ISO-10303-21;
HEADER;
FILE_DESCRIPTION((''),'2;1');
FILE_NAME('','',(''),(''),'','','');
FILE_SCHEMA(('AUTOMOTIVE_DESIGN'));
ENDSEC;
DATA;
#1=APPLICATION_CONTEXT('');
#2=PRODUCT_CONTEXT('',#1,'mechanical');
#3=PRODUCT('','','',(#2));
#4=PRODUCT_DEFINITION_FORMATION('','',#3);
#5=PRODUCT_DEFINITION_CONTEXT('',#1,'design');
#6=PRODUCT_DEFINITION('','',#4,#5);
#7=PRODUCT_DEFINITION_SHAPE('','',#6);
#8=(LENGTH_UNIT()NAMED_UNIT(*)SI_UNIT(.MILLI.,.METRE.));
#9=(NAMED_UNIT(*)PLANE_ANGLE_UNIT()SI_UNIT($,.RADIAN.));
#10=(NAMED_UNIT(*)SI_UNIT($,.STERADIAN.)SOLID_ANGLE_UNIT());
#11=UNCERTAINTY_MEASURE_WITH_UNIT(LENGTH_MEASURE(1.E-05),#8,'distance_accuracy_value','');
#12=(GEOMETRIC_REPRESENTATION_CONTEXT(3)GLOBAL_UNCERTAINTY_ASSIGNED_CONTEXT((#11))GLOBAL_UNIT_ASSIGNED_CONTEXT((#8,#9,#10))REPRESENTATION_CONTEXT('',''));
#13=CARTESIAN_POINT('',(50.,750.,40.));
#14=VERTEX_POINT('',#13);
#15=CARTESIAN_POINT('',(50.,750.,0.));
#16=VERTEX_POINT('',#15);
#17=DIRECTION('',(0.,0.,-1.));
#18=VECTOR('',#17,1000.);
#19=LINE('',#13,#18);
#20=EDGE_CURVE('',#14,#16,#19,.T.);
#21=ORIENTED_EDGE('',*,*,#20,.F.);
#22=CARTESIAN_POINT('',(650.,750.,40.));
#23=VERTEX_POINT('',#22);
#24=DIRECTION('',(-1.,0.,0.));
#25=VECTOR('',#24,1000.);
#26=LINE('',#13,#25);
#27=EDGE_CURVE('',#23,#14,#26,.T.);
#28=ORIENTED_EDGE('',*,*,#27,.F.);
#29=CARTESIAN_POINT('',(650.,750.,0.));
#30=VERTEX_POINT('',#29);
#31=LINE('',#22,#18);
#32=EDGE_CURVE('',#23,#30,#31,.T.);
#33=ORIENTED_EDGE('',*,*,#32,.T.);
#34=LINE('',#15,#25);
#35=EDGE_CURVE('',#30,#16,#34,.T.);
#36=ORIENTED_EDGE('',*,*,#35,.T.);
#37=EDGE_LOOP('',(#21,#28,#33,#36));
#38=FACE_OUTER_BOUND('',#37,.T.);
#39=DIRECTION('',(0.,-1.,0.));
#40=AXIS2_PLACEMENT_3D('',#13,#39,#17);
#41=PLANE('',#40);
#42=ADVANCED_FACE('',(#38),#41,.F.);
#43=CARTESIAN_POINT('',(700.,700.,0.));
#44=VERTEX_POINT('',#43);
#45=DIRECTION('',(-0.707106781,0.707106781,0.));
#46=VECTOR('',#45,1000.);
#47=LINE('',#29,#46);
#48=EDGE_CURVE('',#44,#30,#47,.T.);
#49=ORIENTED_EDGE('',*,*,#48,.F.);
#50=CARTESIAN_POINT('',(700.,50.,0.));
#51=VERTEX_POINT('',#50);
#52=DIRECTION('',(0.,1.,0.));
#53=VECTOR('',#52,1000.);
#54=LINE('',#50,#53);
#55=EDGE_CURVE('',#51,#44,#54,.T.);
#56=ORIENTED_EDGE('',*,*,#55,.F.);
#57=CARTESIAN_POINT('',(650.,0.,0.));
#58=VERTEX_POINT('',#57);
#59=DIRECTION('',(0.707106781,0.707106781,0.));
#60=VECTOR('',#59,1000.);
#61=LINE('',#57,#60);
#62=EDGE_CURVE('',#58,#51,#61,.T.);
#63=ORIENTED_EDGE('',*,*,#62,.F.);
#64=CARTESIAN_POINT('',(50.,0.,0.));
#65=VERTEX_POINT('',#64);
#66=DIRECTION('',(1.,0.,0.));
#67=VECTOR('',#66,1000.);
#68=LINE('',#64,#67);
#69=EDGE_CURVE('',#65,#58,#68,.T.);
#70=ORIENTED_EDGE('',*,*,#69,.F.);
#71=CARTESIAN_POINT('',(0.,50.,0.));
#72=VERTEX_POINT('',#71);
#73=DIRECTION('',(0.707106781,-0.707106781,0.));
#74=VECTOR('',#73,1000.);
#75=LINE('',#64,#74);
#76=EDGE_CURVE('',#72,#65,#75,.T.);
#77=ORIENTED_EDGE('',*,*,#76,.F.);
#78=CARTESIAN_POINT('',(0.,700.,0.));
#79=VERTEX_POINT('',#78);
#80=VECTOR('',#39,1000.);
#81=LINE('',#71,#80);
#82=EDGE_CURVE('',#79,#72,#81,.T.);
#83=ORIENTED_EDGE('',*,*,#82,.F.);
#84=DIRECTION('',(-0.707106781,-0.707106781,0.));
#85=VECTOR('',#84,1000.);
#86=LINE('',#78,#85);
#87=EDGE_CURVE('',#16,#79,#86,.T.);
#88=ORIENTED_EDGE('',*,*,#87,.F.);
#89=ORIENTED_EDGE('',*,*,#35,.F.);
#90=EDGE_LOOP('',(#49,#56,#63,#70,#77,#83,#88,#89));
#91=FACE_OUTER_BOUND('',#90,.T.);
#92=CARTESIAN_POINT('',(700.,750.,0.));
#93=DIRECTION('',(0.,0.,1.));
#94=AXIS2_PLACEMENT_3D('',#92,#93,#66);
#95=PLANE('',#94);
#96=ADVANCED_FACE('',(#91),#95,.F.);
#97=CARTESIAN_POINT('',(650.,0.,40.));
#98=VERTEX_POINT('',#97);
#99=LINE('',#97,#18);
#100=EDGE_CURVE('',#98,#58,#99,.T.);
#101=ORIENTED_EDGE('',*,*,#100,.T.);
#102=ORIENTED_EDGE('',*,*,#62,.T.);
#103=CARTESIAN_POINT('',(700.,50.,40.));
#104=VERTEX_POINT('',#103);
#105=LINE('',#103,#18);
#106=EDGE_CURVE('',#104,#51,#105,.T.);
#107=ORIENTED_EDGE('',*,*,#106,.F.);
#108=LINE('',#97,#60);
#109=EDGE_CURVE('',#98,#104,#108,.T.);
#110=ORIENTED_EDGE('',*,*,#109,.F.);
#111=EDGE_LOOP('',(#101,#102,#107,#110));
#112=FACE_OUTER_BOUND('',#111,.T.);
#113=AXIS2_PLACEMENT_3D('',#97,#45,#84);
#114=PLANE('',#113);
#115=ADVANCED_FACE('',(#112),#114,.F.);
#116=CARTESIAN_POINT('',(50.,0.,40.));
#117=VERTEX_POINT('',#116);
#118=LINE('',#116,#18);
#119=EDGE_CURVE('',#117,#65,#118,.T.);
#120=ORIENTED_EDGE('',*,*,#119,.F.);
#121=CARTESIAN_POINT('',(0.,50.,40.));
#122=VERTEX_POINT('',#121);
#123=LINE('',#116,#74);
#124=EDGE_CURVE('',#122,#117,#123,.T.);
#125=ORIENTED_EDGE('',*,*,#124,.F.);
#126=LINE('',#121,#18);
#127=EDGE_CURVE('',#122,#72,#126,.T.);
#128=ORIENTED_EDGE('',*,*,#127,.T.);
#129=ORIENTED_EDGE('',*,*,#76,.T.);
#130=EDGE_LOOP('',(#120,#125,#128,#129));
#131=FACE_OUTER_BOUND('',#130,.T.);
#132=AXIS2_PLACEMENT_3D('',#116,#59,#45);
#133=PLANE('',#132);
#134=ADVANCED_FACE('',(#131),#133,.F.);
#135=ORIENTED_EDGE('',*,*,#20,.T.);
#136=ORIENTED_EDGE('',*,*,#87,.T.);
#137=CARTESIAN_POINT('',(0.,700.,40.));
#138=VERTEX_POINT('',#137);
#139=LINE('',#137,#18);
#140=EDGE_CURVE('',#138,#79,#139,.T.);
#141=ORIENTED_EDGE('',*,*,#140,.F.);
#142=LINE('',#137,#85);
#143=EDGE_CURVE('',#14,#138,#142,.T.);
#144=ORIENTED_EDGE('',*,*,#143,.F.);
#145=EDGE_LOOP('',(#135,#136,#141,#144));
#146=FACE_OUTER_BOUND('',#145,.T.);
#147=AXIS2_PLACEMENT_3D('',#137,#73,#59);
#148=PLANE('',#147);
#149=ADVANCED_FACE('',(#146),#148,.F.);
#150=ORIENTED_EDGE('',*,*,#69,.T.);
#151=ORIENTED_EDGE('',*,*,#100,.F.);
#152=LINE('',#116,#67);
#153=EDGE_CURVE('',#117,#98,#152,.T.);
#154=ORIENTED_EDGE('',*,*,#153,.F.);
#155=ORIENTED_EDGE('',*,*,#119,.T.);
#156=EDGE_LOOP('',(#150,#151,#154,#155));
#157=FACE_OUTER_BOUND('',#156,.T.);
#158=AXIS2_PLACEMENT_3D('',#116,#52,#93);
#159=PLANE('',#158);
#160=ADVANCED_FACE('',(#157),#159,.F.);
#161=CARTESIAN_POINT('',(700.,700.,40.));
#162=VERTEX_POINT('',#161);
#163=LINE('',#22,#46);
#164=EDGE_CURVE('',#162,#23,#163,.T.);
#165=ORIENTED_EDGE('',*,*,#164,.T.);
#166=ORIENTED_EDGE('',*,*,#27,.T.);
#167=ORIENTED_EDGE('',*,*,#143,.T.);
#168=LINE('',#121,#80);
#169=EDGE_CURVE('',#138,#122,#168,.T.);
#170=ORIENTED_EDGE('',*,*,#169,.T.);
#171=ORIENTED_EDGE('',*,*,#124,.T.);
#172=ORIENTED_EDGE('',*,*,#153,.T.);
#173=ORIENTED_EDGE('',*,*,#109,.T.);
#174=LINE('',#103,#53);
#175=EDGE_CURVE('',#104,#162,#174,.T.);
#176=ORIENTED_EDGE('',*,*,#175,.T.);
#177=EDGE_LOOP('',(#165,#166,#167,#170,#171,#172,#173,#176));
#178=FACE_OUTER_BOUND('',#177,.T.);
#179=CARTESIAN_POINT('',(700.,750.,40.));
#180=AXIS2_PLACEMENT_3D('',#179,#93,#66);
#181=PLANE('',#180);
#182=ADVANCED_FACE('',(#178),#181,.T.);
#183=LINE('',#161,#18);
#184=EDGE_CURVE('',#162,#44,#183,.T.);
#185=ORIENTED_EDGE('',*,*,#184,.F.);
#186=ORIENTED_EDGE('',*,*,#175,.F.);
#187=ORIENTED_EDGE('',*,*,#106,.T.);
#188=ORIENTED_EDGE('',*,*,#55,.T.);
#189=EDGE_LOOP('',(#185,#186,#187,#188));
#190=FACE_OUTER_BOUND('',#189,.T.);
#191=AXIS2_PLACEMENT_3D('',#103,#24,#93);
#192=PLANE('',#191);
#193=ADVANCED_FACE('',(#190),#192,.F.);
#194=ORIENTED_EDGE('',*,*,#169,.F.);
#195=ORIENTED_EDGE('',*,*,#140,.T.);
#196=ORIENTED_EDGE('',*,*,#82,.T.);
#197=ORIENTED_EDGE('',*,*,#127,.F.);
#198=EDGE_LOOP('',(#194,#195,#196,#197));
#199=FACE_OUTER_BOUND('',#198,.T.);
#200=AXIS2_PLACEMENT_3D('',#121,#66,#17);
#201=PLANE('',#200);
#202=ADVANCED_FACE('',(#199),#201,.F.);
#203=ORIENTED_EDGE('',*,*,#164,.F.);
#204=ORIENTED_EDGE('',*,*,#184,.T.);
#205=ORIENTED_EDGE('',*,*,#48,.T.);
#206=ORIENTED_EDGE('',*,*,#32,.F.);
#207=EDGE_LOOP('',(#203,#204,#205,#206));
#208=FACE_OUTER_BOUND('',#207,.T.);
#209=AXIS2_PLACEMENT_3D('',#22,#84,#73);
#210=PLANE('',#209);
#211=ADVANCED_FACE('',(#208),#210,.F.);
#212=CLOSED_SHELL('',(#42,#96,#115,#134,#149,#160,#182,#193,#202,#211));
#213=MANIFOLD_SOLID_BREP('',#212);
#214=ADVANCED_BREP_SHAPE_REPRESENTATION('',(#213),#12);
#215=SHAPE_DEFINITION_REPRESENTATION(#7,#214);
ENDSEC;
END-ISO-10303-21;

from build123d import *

# Parameters (mm, degrees)
EXTRUDE_1_DEPTH = 40


with BuildPart() as part:
    # 草图2 → 凸台-拉伸1 (new body)
    with BuildSketch(Plane.XY):
        Polygon((0, 700), (50, 750), (650, 750), (700, 700), (700, 50), (650, 0), (50, 0), (0, 50), align=None)
    extrude(amount=EXTRUDE_1_DEPTH)


solid = part.part
